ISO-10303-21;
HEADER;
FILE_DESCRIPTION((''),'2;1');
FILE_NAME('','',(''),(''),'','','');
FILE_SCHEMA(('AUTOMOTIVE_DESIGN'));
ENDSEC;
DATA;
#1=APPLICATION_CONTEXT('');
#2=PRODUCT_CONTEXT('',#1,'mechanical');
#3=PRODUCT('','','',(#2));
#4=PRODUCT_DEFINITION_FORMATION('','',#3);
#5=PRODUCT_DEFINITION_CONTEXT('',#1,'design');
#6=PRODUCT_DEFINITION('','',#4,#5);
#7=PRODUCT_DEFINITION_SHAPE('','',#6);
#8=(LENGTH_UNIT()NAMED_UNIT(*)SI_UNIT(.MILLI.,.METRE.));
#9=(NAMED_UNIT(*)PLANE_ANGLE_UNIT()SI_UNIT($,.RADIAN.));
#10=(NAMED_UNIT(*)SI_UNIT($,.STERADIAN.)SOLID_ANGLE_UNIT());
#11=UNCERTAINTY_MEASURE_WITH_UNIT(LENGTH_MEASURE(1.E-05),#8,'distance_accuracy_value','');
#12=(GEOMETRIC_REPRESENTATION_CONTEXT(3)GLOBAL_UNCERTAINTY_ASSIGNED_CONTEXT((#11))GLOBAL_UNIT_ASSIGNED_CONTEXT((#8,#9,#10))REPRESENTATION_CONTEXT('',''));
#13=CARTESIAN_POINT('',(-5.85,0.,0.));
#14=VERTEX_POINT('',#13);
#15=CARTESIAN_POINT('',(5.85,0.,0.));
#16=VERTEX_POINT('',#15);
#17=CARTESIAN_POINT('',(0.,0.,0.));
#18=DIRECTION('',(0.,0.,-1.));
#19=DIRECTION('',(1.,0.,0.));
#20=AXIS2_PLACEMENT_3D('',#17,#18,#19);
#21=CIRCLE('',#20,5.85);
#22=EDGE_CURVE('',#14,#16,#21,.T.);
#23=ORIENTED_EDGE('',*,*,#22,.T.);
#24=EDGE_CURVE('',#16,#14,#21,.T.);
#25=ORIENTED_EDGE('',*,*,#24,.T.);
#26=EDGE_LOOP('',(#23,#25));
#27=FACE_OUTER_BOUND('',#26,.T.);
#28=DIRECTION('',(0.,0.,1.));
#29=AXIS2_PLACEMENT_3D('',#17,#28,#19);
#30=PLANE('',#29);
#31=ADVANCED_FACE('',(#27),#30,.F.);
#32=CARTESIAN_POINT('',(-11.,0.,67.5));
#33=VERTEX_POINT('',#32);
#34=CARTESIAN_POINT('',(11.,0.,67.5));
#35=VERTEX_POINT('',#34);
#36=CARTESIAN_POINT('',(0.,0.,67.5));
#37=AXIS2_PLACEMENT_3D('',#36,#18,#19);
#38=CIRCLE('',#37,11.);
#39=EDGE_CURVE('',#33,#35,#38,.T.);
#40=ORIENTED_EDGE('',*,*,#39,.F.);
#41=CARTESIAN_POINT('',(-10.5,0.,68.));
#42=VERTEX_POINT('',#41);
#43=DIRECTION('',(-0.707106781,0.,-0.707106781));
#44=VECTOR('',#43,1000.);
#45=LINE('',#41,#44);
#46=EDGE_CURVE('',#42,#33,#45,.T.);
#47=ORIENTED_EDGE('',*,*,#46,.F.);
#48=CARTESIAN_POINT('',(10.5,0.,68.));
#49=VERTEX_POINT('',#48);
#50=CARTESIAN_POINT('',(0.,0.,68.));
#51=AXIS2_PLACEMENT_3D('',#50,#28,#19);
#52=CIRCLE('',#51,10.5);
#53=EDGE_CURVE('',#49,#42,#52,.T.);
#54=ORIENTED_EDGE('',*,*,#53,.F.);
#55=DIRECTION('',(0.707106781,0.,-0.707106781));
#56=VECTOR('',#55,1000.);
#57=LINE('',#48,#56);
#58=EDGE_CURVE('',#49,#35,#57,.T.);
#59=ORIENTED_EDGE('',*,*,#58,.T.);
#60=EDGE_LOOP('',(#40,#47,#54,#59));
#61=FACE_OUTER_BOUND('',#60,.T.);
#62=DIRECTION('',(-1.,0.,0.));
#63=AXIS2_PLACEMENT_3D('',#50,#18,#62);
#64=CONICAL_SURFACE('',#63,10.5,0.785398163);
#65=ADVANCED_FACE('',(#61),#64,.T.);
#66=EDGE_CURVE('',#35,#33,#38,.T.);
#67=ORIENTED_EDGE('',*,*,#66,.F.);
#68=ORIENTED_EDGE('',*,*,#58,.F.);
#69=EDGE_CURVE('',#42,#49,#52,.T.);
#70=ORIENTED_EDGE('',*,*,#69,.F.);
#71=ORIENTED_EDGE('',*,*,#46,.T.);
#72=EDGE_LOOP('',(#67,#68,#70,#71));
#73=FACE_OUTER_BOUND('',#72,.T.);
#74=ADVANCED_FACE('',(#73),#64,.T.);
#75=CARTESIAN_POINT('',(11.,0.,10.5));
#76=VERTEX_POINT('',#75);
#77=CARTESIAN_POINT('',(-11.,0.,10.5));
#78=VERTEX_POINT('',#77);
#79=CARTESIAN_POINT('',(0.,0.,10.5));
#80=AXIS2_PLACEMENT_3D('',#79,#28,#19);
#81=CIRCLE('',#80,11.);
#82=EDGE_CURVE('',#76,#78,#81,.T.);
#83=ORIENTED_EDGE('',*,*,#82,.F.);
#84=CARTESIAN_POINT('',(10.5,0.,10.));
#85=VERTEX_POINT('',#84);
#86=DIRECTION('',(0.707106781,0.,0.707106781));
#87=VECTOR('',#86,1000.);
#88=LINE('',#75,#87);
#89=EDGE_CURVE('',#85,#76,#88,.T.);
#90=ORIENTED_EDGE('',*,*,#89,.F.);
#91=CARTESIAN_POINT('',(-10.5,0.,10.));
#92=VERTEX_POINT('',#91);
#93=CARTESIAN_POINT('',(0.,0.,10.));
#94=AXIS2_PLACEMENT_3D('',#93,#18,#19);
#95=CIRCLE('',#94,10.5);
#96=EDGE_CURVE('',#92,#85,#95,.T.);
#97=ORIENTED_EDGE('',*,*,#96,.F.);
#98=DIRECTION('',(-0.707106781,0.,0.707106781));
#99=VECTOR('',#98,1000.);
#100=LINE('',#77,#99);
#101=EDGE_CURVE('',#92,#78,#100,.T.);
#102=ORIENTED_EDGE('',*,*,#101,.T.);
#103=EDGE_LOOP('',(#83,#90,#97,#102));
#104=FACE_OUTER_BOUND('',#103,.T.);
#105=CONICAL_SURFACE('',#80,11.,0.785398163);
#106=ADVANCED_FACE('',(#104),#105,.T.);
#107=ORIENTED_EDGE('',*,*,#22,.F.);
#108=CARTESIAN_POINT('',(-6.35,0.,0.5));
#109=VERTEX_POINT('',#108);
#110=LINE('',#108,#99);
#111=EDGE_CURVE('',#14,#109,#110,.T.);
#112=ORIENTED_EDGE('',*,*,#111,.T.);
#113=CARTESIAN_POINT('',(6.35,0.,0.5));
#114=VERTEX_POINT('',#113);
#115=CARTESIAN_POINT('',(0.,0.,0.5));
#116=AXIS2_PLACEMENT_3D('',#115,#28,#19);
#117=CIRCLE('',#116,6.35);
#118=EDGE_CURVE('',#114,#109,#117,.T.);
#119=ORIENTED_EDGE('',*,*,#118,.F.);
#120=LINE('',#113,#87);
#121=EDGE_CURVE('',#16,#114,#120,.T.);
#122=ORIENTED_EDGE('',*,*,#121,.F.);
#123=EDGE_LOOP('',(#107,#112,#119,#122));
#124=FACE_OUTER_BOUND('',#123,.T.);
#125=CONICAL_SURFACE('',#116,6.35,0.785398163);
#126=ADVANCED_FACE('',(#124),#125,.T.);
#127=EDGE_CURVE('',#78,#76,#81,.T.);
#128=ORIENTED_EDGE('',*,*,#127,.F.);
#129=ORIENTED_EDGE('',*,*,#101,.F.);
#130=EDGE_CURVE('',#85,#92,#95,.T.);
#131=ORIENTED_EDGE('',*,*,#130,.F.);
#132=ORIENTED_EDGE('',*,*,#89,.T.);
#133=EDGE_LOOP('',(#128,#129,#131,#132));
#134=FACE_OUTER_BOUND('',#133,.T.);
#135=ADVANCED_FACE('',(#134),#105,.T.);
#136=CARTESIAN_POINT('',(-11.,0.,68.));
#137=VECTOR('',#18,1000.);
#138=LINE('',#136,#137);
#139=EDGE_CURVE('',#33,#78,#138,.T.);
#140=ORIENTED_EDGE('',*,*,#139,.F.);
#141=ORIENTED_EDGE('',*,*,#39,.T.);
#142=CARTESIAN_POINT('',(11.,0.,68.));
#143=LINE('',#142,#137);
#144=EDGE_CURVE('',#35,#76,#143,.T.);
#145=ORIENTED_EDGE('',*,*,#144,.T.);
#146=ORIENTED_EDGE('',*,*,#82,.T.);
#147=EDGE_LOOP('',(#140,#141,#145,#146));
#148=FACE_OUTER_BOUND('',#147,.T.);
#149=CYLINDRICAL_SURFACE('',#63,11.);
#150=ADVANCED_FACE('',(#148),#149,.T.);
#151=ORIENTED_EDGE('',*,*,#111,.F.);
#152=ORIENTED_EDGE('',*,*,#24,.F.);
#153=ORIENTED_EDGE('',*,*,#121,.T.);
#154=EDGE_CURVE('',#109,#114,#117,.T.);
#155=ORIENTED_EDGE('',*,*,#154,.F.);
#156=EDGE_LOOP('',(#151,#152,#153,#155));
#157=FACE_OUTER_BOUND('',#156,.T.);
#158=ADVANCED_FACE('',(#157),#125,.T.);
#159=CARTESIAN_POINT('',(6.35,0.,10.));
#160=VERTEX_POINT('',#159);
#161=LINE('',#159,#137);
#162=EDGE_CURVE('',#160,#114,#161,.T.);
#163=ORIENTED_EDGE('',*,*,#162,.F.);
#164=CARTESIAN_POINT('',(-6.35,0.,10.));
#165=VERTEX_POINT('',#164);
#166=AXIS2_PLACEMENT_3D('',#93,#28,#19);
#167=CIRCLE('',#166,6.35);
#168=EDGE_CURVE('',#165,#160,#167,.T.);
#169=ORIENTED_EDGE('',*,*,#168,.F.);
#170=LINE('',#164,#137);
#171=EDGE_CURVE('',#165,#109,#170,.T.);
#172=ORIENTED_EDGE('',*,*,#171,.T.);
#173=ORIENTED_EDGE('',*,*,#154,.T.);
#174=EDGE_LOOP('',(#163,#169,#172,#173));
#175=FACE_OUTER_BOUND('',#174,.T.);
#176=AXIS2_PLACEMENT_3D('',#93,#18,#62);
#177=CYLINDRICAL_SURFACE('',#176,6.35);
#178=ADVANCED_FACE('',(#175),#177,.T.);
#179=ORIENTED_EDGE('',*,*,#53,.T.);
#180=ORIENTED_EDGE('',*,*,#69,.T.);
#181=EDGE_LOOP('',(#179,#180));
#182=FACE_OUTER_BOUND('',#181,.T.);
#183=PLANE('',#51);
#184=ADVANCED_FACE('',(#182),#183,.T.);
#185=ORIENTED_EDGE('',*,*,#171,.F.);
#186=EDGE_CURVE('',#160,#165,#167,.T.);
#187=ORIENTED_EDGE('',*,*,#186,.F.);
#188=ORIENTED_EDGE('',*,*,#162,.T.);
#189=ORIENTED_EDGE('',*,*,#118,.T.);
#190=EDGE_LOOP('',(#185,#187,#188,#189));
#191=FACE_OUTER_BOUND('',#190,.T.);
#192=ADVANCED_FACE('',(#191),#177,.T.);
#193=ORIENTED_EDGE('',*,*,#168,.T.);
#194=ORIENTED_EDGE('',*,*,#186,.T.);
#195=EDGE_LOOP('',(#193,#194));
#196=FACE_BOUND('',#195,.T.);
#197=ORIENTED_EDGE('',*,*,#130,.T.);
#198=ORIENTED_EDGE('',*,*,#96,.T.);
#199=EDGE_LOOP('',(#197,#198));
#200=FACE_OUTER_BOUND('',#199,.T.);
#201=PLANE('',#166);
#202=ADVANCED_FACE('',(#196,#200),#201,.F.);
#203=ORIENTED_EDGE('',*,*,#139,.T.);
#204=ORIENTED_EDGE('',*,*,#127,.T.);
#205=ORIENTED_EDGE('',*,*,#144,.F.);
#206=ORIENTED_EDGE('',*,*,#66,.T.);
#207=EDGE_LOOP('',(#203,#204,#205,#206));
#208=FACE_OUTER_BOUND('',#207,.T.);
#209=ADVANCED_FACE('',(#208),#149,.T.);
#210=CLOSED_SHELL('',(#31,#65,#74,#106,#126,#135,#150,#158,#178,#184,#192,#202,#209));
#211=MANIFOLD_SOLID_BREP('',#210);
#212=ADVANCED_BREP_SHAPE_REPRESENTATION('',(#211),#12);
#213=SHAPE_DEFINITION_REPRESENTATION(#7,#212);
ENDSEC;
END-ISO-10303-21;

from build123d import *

# Parameters (mm, degrees)
SKETCH1_R           = 6.35
BOSS_EXTRUDE1_DEPTH = 10
SKETCH2_R           = 11
BOSS_EXTRUDE2_DEPTH = 58
CHAMFER1_SIZE       = 0.5


with BuildPart() as part:
    # Sketch1 → Boss-Extrude1 (new body)
    with BuildSketch(Plane.XY):
        Circle(SKETCH1_R)
    extrude(amount=BOSS_EXTRUDE1_DEPTH)

    # Sketch2 → Boss-Extrude2 (add)
    with BuildSketch(Plane.XY.offset(10)):
        Circle(SKETCH2_R)
    extrude(amount=BOSS_EXTRUDE2_DEPTH)

    # Chamfer1
    chamfer1_edges = [part.edges().sort_by_distance(p)[0] for p in [
        (-6.35, 0, 0),
        (-11, 0, 10),
        (-11, 0, 68),
    ]]
    chamfer(chamfer1_edges, length=CHAMFER1_SIZE)


solid = part.part
